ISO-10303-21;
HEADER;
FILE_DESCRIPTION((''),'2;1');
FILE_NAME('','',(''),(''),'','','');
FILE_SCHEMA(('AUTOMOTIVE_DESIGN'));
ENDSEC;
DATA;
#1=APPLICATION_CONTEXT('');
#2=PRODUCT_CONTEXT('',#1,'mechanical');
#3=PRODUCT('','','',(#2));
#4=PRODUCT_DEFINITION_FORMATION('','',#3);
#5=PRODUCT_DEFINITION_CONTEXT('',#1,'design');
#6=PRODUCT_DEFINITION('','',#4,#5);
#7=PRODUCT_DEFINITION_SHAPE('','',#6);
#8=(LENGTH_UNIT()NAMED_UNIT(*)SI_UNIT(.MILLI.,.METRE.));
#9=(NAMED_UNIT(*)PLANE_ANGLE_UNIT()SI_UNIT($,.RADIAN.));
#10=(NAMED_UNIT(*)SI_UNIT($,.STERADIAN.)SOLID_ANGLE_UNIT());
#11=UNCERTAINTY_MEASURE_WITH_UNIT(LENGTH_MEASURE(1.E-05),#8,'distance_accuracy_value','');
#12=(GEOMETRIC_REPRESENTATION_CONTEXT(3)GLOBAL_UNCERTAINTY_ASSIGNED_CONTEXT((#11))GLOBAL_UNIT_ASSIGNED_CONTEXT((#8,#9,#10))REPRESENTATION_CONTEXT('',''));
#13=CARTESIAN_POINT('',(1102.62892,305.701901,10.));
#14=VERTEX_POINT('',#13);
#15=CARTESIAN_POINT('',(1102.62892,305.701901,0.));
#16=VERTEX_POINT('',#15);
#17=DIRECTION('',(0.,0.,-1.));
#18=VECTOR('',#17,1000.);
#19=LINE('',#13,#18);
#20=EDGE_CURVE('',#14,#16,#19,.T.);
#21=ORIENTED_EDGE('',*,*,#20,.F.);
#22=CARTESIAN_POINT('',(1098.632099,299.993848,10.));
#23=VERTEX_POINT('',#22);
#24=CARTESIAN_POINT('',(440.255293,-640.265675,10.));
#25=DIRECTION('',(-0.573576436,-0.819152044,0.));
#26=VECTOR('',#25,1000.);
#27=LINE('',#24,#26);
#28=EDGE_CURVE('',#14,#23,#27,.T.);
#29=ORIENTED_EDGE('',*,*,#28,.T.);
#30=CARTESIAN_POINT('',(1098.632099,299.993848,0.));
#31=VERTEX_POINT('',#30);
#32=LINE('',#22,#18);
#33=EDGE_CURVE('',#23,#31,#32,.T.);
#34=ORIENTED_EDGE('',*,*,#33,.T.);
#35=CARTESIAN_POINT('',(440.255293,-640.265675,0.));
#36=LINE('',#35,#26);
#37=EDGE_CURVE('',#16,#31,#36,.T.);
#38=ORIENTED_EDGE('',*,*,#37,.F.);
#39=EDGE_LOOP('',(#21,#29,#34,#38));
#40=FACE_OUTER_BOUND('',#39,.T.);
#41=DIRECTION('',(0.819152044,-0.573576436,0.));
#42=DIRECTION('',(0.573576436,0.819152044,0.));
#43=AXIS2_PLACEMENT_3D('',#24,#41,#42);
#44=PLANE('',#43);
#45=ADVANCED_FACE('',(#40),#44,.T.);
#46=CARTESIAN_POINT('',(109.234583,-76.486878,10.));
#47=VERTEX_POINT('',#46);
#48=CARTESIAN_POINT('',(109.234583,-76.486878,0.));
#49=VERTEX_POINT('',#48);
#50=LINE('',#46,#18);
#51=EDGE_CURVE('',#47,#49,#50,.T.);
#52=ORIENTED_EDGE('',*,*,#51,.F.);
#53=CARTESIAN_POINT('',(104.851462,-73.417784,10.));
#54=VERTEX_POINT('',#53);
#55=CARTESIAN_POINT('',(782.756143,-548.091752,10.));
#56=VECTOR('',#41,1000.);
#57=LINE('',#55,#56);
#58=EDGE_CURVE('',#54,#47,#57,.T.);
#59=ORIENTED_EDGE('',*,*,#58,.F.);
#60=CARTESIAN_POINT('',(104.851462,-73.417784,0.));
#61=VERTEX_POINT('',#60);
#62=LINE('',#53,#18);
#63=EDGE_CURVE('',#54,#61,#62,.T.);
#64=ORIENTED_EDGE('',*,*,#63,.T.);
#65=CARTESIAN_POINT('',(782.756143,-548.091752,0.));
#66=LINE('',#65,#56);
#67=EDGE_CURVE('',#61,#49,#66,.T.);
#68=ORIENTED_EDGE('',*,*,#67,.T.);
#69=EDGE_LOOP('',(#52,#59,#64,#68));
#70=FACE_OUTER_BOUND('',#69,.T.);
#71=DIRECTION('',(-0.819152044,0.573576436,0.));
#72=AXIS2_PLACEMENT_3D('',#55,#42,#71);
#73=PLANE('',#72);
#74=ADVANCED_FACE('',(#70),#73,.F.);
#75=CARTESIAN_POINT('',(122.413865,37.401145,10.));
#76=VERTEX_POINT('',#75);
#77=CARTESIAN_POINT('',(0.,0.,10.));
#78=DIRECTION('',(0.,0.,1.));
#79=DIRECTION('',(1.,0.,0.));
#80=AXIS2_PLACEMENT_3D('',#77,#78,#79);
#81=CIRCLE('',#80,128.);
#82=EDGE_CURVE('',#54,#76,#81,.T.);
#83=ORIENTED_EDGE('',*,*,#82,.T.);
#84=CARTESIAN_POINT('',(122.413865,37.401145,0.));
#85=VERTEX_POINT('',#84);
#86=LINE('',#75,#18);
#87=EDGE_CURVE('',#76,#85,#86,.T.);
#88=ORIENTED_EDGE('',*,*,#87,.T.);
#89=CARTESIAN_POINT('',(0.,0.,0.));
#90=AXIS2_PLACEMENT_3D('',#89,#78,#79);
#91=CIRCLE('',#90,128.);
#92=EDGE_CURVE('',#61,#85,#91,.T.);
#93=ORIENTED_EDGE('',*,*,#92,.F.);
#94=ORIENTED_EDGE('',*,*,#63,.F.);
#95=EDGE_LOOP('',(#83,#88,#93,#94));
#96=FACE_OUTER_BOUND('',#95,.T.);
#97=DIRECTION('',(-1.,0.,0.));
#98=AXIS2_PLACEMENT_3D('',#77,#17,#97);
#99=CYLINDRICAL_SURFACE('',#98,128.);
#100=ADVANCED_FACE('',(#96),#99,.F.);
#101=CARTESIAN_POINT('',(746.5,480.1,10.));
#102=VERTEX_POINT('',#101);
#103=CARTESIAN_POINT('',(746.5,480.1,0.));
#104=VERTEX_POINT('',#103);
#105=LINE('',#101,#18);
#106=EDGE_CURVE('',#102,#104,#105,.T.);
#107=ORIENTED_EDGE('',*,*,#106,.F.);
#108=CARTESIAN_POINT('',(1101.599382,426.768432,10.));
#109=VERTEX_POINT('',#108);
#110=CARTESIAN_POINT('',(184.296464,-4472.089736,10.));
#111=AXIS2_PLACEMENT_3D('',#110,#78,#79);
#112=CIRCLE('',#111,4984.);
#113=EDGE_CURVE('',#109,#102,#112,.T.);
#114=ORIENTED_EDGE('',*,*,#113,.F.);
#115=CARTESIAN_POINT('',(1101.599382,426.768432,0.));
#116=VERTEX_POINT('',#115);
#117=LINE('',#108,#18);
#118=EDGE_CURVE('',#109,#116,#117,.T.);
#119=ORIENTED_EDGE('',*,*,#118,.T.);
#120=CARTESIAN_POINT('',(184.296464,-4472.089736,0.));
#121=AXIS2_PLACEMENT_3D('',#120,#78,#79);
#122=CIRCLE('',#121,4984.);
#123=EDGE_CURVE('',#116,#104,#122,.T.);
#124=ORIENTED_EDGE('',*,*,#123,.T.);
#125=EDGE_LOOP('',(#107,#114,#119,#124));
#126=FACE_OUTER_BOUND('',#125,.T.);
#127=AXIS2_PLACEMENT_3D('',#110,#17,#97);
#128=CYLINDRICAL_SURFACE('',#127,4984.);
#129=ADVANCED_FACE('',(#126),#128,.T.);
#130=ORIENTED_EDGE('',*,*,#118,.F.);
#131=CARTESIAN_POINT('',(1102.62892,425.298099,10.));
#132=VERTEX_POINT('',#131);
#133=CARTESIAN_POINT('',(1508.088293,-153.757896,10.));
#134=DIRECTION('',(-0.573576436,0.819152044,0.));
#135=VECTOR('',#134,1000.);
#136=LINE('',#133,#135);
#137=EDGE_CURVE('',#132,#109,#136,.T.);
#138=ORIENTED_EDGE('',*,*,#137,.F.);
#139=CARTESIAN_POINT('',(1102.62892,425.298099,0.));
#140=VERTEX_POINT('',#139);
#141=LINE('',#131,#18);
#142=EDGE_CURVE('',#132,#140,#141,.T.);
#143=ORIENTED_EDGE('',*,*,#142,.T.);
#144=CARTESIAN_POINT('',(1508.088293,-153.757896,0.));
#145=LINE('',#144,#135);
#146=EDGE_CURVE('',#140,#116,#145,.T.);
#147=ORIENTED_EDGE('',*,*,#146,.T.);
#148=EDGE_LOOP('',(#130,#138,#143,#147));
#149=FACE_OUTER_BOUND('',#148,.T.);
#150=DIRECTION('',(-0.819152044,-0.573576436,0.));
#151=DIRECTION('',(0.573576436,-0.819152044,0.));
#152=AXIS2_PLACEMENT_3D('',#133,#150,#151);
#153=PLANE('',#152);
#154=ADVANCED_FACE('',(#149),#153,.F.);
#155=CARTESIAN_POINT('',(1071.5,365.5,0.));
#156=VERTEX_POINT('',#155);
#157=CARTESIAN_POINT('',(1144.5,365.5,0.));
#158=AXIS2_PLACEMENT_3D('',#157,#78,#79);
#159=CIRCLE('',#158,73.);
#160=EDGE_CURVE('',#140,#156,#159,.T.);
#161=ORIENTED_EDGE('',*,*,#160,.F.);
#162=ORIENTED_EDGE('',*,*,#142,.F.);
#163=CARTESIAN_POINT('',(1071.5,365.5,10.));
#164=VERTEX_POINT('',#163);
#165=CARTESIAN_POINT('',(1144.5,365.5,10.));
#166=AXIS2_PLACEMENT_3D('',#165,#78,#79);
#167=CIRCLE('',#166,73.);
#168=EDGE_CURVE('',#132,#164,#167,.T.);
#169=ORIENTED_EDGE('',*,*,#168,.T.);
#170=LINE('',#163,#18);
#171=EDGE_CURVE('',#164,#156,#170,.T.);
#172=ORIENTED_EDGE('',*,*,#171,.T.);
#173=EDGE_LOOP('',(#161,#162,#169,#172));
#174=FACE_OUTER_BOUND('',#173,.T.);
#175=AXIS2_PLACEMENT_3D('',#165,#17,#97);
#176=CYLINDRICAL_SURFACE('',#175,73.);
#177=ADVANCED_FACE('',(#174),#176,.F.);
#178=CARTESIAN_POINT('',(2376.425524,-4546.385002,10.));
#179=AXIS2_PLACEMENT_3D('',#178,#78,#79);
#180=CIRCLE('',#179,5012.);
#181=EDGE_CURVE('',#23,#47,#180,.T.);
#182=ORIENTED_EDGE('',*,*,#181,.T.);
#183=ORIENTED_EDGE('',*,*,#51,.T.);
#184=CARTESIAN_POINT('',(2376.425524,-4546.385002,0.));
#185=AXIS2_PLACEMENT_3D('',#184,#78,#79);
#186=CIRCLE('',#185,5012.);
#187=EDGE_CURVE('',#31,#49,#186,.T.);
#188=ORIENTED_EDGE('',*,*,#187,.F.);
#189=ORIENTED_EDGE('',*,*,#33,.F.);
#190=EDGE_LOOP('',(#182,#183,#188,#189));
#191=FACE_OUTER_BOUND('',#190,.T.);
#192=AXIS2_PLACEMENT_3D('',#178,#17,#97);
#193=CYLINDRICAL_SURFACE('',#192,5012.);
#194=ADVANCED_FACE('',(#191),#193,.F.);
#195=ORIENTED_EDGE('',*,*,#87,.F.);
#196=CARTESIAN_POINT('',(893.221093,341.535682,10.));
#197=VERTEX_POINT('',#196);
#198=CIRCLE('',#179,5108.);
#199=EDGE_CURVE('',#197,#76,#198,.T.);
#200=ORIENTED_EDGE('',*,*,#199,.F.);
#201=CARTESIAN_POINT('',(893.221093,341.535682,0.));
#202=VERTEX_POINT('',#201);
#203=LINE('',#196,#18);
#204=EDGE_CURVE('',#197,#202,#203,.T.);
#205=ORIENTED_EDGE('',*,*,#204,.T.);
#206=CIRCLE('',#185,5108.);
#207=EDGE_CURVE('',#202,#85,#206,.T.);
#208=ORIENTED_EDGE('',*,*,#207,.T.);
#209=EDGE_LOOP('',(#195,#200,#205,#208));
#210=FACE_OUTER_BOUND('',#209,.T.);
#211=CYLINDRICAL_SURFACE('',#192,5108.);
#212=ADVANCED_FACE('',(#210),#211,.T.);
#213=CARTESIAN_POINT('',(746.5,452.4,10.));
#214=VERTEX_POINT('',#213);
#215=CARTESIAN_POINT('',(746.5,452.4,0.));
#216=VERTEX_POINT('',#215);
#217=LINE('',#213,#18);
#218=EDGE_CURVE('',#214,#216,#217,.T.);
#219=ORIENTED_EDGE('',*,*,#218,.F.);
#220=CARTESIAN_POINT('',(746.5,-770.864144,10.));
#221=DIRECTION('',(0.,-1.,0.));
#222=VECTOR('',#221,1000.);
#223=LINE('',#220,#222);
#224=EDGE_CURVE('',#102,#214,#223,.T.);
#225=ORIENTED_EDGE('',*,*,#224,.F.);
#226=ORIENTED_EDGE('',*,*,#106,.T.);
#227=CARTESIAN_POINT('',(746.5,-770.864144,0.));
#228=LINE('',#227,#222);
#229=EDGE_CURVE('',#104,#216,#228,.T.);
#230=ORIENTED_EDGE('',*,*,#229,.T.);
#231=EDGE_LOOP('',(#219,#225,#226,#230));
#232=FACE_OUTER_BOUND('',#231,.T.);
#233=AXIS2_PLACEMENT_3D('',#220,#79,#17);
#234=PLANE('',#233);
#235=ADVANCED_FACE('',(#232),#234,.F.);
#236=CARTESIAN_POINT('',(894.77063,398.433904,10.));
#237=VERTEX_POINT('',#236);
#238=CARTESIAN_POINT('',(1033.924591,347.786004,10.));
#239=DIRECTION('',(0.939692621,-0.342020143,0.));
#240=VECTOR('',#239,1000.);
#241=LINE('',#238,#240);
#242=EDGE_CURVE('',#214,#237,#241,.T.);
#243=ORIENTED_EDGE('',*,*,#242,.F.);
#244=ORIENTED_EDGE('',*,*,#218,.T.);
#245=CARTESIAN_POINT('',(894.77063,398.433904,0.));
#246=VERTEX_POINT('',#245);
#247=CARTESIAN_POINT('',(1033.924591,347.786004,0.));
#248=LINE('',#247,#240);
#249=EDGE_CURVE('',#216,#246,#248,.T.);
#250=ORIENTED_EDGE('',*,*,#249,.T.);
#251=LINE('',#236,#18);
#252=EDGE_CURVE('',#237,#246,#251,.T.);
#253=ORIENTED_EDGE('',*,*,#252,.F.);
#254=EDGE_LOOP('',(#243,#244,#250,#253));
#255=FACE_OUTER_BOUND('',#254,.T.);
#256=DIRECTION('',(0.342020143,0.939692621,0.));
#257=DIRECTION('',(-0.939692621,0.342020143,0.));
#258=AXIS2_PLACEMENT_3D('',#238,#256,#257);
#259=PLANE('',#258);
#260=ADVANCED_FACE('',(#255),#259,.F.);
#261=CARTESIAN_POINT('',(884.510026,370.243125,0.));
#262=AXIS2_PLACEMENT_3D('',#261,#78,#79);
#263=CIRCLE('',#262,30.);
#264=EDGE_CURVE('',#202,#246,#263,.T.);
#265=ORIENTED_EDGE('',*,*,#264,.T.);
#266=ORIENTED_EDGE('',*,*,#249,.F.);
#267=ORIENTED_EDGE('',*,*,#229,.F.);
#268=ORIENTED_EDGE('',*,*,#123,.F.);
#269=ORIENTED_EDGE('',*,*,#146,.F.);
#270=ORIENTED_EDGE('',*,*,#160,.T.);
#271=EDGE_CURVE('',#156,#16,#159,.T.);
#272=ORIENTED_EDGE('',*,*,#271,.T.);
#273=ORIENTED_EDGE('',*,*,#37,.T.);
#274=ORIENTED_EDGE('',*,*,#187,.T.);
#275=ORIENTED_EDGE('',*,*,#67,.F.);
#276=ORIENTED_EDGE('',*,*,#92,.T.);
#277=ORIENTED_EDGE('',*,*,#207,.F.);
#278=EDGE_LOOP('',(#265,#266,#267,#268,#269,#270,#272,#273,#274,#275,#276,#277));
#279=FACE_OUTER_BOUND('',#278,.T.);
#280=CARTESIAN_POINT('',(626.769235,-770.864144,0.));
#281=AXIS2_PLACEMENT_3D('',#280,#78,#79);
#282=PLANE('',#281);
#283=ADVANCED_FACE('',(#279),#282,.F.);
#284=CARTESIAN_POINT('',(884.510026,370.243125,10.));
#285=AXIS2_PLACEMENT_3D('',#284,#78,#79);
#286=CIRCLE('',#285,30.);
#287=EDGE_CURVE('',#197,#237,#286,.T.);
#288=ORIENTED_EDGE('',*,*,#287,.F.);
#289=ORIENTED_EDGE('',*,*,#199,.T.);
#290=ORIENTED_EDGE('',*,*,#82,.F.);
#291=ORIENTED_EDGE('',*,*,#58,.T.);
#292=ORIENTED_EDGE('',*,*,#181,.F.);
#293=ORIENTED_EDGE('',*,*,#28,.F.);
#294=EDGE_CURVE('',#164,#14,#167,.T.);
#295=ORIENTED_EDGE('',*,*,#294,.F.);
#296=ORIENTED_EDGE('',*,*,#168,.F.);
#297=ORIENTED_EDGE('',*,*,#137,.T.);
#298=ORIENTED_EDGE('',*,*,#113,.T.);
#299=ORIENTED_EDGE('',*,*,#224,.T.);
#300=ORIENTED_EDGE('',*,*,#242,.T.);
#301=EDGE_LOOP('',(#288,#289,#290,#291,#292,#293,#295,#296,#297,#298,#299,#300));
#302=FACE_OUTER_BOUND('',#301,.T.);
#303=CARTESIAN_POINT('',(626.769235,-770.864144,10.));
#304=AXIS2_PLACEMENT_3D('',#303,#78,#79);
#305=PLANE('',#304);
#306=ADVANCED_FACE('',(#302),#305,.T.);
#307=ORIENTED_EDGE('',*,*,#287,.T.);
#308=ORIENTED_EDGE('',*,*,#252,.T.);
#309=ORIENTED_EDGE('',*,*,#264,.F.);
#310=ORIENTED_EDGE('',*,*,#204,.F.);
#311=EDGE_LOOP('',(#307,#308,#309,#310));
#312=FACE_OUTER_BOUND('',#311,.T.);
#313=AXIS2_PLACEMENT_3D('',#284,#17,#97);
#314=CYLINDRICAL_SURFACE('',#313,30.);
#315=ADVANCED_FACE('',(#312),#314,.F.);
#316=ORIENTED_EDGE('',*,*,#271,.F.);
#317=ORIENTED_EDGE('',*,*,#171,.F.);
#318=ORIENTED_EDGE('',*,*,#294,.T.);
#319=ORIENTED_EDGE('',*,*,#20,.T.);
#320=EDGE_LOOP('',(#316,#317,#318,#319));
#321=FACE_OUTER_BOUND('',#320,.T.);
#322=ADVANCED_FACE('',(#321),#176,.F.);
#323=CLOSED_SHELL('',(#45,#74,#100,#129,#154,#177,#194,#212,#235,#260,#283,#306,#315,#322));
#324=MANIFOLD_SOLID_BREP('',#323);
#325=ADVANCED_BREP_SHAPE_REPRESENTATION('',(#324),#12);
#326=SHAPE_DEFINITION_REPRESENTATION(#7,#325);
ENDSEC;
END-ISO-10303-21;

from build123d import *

# Parameters (mm, degrees)
BOSS_EXTRUDE1_DEPTH = 10


with BuildPart() as part:
    # Sketch1 → Boss-Extrude1 (new body)
    with BuildSketch(Plane.XY):
        with BuildLine():
            ThreePointArc((893.221093202, 341.53568212), (914.498906919, 369.426423756), (894.770629974, 398.433904074))
            Line((894.770629974, 398.433904074), (746.5, 452.4))
            Line((746.5, 452.4), (746.5, 480.1))
            ThreePointArc((746.5, 480.1), (924.530143798, 456.633232126), (1101.599381764, 426.768432422))
            Line((1101.599381764, 426.768432422), (1102.628920146, 425.298099233))
            ThreePointArc((1102.628920146, 425.298099233), (1071.5, 365.5), (1102.628920146, 305.701900767))
            Line((1102.628920146, 305.701900767), (1098.632098759, 299.99384827))
            ThreePointArc((1098.632098759, 299.99384827), (593.965714202, 137.948571105), (109.234583042, -76.486878479))
            Line((109.234583042, -76.486878479), (104.851461669, -73.417783853))
            ThreePointArc((104.851461669, -73.417783853), (126.422272258, -20.035195957), (122.413865115, 37.401144736))
            ThreePointArc((122.413865115, 37.401144736), (501.640075089, 205.12460213), (893.221093202, 341.53568212))
        make_face()
    extrude(amount=BOSS_EXTRUDE1_DEPTH)


solid = part.part
